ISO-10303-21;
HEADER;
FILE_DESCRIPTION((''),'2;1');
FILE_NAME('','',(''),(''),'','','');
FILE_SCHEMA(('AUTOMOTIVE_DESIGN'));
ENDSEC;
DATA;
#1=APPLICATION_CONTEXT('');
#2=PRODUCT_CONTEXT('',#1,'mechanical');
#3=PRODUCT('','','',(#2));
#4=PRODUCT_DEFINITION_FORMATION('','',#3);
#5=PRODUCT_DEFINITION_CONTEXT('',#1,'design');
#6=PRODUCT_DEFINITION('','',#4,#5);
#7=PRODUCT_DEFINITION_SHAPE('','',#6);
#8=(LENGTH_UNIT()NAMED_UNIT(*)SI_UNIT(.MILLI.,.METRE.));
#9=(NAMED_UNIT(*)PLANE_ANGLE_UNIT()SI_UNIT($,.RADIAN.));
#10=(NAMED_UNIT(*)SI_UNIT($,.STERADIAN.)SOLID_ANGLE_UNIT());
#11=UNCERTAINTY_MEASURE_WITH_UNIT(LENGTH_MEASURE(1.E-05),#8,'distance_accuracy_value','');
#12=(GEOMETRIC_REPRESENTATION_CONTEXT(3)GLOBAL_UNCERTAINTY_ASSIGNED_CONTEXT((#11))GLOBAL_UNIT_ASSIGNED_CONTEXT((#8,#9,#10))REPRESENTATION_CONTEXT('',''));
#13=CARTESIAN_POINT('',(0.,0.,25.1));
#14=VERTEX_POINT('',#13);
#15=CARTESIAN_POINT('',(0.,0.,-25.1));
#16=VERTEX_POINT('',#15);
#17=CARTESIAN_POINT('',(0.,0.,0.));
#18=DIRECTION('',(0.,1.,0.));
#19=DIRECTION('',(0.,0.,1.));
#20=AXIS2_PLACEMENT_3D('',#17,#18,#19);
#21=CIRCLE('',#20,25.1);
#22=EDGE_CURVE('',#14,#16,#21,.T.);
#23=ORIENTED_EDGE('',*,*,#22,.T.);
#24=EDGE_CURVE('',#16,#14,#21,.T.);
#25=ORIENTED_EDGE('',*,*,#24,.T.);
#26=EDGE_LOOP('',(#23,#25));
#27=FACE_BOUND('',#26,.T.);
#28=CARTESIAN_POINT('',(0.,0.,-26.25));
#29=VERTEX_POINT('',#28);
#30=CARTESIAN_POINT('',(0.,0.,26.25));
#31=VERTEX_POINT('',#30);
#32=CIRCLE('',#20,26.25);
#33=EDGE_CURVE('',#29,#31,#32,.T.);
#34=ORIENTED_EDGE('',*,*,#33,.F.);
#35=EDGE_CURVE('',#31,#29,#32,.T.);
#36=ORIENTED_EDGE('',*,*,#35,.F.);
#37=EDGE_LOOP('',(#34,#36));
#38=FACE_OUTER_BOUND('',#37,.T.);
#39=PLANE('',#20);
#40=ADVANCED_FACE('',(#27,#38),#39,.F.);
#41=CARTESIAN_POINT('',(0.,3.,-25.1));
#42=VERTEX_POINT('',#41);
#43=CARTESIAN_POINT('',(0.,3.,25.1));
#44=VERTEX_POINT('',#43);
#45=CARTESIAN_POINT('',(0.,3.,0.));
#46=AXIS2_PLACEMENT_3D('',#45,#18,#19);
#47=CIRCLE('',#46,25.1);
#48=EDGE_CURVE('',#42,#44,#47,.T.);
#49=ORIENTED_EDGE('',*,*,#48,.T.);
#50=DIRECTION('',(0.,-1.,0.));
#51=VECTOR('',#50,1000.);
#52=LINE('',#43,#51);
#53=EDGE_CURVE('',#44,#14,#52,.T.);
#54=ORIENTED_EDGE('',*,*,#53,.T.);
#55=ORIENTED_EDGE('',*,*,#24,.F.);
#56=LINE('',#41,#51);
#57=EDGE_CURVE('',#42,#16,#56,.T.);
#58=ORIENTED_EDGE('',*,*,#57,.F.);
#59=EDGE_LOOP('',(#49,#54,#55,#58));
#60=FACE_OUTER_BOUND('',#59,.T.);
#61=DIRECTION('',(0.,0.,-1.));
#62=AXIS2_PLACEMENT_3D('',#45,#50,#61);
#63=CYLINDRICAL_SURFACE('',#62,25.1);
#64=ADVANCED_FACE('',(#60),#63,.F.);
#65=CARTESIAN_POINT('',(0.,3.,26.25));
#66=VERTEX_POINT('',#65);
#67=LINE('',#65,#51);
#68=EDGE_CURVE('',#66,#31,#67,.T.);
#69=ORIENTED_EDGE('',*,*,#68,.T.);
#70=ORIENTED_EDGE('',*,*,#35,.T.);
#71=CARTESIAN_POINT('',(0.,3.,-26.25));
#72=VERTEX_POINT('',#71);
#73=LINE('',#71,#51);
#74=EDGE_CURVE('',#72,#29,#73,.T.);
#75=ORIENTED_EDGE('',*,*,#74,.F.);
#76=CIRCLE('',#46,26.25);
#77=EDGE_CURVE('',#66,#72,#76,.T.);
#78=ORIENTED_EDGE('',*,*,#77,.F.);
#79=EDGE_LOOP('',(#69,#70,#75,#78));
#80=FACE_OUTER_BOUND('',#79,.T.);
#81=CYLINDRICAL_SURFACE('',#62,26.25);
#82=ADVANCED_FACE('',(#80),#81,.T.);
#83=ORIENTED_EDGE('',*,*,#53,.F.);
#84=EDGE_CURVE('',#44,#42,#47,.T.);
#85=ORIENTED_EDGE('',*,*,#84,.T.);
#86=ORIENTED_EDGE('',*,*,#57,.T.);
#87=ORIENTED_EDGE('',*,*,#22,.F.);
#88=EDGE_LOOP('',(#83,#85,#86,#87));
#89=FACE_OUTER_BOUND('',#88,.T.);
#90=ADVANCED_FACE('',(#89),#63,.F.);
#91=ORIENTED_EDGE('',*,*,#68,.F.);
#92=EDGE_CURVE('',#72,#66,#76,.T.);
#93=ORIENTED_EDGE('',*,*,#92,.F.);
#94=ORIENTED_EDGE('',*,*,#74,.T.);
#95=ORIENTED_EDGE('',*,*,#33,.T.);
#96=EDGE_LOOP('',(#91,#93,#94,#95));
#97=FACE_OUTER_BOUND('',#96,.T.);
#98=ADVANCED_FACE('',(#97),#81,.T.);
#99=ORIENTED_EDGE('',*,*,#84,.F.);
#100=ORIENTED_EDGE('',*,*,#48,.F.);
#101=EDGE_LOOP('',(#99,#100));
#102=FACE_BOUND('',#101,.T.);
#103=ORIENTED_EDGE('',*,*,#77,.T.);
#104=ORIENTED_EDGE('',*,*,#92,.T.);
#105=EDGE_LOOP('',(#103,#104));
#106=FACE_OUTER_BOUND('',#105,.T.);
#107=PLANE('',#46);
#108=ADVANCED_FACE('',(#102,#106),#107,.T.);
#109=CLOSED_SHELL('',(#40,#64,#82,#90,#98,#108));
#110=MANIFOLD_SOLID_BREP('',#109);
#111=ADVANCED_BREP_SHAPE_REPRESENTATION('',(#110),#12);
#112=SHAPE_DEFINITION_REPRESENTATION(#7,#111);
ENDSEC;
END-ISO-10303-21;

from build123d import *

# Parameters (mm, degrees)
SKETCH1_R           = 26.25
SKETCH1_R_2         = 25.1
BOSS_EXTRUDE1_DEPTH = 3


with BuildPart() as part:
    # Sketch1 → Boss-Extrude1 (new body)
    with BuildSketch(Plane(origin=(0, 0, 0), x_dir=(1, 0, 0), z_dir=(0, 1, 0))):
        with Locations(Location((0, 0, 0), (0, 0, 270))):
            Circle(SKETCH1_R)
        with Locations(Location((0, 0, 0), (0, 0, 270))):
            Circle(SKETCH1_R_2, mode=Mode.SUBTRACT)
    extrude(amount=BOSS_EXTRUDE1_DEPTH)


solid = part.part
